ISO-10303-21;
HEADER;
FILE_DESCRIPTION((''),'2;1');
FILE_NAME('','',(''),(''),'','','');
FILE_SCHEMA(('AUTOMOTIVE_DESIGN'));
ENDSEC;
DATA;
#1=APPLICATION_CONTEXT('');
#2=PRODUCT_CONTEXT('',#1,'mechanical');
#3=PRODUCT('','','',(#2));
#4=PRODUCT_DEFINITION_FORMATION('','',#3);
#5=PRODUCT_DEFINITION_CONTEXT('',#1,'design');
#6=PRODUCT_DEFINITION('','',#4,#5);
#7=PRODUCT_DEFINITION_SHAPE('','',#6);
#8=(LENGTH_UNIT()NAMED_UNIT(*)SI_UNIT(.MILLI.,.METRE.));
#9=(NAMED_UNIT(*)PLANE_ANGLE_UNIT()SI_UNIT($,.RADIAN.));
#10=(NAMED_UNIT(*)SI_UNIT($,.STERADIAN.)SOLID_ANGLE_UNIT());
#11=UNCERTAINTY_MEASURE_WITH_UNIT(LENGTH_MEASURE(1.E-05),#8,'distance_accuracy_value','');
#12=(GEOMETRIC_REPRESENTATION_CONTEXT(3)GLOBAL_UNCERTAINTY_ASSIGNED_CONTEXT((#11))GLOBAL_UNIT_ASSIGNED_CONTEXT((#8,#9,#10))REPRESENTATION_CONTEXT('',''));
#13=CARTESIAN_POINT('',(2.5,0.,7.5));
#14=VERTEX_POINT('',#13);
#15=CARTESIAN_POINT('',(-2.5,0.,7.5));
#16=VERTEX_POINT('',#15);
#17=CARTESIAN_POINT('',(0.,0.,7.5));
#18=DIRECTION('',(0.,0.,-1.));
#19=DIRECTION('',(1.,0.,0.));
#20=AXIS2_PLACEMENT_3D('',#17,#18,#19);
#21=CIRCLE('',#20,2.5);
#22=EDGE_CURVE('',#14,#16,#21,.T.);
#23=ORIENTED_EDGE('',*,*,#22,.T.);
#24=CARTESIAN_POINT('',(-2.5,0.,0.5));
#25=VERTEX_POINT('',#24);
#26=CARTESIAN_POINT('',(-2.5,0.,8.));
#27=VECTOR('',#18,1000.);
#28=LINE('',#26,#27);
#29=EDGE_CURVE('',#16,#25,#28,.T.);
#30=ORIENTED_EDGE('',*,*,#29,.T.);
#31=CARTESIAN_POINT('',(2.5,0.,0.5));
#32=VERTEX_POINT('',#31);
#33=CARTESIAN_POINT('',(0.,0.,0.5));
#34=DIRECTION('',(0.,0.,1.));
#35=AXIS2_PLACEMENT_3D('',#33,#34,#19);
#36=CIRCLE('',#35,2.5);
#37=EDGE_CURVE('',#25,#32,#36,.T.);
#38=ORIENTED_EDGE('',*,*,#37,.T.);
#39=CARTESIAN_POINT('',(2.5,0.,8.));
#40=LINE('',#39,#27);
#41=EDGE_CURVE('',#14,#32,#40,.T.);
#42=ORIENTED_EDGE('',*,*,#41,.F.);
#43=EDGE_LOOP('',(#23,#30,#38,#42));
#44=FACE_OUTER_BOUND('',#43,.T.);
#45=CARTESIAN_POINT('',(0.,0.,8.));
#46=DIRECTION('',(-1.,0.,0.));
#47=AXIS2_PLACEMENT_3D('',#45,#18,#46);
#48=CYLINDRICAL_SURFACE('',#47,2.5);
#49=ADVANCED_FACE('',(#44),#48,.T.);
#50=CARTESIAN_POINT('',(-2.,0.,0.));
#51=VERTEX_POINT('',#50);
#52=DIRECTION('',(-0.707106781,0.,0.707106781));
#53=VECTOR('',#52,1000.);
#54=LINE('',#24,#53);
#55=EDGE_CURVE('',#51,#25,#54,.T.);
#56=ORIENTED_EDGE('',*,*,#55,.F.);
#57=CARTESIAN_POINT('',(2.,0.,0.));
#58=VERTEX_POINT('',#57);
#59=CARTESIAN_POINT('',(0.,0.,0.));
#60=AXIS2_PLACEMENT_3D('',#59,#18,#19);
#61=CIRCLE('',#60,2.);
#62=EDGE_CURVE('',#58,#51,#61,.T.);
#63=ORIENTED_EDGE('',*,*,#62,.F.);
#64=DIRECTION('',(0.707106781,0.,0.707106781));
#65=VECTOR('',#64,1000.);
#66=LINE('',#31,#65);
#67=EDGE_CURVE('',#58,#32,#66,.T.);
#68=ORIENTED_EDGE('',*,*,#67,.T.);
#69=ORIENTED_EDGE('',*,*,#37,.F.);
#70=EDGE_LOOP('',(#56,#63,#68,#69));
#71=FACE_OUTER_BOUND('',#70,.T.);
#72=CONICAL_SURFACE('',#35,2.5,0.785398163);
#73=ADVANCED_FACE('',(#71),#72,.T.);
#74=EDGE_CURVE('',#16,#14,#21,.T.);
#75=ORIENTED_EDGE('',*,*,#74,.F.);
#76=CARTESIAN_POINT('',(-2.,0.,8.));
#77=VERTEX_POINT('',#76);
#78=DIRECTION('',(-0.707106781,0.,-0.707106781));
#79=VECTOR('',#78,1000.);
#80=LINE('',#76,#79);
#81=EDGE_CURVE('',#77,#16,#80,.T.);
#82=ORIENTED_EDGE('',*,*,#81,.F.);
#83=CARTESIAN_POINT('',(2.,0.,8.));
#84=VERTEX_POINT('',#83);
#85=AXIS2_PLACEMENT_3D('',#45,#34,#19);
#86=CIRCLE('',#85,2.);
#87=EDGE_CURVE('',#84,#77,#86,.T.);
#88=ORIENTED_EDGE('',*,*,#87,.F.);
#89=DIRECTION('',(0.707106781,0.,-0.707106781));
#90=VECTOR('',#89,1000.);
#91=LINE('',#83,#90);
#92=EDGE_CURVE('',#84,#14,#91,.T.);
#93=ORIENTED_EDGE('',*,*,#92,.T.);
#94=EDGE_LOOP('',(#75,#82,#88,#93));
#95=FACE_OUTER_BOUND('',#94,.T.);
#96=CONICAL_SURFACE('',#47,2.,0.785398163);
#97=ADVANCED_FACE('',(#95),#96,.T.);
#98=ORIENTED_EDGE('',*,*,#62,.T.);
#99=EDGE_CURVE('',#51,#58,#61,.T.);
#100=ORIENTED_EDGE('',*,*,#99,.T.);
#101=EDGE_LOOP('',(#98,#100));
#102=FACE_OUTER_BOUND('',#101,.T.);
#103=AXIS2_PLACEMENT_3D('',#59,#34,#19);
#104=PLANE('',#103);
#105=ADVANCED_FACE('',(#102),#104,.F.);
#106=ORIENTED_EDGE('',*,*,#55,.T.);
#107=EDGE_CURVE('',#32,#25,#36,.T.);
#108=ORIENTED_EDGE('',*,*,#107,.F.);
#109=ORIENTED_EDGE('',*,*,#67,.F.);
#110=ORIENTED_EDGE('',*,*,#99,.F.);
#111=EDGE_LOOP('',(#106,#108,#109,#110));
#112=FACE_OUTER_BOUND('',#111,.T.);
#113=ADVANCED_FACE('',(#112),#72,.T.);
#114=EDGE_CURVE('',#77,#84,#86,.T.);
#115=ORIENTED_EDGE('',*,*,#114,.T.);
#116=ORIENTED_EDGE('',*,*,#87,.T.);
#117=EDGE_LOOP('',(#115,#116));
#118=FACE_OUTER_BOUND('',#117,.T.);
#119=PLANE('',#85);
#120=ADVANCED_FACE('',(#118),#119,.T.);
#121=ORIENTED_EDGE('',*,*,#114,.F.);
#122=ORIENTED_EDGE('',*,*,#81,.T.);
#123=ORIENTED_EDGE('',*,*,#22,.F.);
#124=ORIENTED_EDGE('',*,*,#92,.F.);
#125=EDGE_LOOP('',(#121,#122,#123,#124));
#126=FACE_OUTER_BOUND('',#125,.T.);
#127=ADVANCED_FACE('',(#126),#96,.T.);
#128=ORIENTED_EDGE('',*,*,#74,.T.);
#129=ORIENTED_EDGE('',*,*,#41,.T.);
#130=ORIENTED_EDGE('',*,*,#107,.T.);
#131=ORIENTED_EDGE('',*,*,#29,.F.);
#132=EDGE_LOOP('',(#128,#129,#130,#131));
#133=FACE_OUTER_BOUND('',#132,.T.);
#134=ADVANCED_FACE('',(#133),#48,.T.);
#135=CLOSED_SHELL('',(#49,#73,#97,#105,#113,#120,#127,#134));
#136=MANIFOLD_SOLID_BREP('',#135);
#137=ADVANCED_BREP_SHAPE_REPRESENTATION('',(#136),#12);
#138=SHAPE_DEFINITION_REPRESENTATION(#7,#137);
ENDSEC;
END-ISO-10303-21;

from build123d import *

# Parameters (mm, degrees)
PIN_PROFILE_5_R          = 2.5
PIN_BODY_5X8_DEPTH       = 8
END_CHAMFERS_0_5X45_SIZE = 0.5


with BuildPart() as part:
    # Pin Profile Ø5 → Pin Body Ø5x8 (new body)
    with BuildSketch(Plane.XY):
        Circle(PIN_PROFILE_5_R)
    extrude(amount=PIN_BODY_5X8_DEPTH)

    # End Chamfers 0.5x45°
    end_chamfers_0_5x45_edges = [part.edges().sort_by_distance(p)[0] for p in [
        (-2.5, 0, 0),
        (-2.5, 0, 8),
    ]]
    chamfer(end_chamfers_0_5x45_edges, length=END_CHAMFERS_0_5X45_SIZE)


solid = part.part
